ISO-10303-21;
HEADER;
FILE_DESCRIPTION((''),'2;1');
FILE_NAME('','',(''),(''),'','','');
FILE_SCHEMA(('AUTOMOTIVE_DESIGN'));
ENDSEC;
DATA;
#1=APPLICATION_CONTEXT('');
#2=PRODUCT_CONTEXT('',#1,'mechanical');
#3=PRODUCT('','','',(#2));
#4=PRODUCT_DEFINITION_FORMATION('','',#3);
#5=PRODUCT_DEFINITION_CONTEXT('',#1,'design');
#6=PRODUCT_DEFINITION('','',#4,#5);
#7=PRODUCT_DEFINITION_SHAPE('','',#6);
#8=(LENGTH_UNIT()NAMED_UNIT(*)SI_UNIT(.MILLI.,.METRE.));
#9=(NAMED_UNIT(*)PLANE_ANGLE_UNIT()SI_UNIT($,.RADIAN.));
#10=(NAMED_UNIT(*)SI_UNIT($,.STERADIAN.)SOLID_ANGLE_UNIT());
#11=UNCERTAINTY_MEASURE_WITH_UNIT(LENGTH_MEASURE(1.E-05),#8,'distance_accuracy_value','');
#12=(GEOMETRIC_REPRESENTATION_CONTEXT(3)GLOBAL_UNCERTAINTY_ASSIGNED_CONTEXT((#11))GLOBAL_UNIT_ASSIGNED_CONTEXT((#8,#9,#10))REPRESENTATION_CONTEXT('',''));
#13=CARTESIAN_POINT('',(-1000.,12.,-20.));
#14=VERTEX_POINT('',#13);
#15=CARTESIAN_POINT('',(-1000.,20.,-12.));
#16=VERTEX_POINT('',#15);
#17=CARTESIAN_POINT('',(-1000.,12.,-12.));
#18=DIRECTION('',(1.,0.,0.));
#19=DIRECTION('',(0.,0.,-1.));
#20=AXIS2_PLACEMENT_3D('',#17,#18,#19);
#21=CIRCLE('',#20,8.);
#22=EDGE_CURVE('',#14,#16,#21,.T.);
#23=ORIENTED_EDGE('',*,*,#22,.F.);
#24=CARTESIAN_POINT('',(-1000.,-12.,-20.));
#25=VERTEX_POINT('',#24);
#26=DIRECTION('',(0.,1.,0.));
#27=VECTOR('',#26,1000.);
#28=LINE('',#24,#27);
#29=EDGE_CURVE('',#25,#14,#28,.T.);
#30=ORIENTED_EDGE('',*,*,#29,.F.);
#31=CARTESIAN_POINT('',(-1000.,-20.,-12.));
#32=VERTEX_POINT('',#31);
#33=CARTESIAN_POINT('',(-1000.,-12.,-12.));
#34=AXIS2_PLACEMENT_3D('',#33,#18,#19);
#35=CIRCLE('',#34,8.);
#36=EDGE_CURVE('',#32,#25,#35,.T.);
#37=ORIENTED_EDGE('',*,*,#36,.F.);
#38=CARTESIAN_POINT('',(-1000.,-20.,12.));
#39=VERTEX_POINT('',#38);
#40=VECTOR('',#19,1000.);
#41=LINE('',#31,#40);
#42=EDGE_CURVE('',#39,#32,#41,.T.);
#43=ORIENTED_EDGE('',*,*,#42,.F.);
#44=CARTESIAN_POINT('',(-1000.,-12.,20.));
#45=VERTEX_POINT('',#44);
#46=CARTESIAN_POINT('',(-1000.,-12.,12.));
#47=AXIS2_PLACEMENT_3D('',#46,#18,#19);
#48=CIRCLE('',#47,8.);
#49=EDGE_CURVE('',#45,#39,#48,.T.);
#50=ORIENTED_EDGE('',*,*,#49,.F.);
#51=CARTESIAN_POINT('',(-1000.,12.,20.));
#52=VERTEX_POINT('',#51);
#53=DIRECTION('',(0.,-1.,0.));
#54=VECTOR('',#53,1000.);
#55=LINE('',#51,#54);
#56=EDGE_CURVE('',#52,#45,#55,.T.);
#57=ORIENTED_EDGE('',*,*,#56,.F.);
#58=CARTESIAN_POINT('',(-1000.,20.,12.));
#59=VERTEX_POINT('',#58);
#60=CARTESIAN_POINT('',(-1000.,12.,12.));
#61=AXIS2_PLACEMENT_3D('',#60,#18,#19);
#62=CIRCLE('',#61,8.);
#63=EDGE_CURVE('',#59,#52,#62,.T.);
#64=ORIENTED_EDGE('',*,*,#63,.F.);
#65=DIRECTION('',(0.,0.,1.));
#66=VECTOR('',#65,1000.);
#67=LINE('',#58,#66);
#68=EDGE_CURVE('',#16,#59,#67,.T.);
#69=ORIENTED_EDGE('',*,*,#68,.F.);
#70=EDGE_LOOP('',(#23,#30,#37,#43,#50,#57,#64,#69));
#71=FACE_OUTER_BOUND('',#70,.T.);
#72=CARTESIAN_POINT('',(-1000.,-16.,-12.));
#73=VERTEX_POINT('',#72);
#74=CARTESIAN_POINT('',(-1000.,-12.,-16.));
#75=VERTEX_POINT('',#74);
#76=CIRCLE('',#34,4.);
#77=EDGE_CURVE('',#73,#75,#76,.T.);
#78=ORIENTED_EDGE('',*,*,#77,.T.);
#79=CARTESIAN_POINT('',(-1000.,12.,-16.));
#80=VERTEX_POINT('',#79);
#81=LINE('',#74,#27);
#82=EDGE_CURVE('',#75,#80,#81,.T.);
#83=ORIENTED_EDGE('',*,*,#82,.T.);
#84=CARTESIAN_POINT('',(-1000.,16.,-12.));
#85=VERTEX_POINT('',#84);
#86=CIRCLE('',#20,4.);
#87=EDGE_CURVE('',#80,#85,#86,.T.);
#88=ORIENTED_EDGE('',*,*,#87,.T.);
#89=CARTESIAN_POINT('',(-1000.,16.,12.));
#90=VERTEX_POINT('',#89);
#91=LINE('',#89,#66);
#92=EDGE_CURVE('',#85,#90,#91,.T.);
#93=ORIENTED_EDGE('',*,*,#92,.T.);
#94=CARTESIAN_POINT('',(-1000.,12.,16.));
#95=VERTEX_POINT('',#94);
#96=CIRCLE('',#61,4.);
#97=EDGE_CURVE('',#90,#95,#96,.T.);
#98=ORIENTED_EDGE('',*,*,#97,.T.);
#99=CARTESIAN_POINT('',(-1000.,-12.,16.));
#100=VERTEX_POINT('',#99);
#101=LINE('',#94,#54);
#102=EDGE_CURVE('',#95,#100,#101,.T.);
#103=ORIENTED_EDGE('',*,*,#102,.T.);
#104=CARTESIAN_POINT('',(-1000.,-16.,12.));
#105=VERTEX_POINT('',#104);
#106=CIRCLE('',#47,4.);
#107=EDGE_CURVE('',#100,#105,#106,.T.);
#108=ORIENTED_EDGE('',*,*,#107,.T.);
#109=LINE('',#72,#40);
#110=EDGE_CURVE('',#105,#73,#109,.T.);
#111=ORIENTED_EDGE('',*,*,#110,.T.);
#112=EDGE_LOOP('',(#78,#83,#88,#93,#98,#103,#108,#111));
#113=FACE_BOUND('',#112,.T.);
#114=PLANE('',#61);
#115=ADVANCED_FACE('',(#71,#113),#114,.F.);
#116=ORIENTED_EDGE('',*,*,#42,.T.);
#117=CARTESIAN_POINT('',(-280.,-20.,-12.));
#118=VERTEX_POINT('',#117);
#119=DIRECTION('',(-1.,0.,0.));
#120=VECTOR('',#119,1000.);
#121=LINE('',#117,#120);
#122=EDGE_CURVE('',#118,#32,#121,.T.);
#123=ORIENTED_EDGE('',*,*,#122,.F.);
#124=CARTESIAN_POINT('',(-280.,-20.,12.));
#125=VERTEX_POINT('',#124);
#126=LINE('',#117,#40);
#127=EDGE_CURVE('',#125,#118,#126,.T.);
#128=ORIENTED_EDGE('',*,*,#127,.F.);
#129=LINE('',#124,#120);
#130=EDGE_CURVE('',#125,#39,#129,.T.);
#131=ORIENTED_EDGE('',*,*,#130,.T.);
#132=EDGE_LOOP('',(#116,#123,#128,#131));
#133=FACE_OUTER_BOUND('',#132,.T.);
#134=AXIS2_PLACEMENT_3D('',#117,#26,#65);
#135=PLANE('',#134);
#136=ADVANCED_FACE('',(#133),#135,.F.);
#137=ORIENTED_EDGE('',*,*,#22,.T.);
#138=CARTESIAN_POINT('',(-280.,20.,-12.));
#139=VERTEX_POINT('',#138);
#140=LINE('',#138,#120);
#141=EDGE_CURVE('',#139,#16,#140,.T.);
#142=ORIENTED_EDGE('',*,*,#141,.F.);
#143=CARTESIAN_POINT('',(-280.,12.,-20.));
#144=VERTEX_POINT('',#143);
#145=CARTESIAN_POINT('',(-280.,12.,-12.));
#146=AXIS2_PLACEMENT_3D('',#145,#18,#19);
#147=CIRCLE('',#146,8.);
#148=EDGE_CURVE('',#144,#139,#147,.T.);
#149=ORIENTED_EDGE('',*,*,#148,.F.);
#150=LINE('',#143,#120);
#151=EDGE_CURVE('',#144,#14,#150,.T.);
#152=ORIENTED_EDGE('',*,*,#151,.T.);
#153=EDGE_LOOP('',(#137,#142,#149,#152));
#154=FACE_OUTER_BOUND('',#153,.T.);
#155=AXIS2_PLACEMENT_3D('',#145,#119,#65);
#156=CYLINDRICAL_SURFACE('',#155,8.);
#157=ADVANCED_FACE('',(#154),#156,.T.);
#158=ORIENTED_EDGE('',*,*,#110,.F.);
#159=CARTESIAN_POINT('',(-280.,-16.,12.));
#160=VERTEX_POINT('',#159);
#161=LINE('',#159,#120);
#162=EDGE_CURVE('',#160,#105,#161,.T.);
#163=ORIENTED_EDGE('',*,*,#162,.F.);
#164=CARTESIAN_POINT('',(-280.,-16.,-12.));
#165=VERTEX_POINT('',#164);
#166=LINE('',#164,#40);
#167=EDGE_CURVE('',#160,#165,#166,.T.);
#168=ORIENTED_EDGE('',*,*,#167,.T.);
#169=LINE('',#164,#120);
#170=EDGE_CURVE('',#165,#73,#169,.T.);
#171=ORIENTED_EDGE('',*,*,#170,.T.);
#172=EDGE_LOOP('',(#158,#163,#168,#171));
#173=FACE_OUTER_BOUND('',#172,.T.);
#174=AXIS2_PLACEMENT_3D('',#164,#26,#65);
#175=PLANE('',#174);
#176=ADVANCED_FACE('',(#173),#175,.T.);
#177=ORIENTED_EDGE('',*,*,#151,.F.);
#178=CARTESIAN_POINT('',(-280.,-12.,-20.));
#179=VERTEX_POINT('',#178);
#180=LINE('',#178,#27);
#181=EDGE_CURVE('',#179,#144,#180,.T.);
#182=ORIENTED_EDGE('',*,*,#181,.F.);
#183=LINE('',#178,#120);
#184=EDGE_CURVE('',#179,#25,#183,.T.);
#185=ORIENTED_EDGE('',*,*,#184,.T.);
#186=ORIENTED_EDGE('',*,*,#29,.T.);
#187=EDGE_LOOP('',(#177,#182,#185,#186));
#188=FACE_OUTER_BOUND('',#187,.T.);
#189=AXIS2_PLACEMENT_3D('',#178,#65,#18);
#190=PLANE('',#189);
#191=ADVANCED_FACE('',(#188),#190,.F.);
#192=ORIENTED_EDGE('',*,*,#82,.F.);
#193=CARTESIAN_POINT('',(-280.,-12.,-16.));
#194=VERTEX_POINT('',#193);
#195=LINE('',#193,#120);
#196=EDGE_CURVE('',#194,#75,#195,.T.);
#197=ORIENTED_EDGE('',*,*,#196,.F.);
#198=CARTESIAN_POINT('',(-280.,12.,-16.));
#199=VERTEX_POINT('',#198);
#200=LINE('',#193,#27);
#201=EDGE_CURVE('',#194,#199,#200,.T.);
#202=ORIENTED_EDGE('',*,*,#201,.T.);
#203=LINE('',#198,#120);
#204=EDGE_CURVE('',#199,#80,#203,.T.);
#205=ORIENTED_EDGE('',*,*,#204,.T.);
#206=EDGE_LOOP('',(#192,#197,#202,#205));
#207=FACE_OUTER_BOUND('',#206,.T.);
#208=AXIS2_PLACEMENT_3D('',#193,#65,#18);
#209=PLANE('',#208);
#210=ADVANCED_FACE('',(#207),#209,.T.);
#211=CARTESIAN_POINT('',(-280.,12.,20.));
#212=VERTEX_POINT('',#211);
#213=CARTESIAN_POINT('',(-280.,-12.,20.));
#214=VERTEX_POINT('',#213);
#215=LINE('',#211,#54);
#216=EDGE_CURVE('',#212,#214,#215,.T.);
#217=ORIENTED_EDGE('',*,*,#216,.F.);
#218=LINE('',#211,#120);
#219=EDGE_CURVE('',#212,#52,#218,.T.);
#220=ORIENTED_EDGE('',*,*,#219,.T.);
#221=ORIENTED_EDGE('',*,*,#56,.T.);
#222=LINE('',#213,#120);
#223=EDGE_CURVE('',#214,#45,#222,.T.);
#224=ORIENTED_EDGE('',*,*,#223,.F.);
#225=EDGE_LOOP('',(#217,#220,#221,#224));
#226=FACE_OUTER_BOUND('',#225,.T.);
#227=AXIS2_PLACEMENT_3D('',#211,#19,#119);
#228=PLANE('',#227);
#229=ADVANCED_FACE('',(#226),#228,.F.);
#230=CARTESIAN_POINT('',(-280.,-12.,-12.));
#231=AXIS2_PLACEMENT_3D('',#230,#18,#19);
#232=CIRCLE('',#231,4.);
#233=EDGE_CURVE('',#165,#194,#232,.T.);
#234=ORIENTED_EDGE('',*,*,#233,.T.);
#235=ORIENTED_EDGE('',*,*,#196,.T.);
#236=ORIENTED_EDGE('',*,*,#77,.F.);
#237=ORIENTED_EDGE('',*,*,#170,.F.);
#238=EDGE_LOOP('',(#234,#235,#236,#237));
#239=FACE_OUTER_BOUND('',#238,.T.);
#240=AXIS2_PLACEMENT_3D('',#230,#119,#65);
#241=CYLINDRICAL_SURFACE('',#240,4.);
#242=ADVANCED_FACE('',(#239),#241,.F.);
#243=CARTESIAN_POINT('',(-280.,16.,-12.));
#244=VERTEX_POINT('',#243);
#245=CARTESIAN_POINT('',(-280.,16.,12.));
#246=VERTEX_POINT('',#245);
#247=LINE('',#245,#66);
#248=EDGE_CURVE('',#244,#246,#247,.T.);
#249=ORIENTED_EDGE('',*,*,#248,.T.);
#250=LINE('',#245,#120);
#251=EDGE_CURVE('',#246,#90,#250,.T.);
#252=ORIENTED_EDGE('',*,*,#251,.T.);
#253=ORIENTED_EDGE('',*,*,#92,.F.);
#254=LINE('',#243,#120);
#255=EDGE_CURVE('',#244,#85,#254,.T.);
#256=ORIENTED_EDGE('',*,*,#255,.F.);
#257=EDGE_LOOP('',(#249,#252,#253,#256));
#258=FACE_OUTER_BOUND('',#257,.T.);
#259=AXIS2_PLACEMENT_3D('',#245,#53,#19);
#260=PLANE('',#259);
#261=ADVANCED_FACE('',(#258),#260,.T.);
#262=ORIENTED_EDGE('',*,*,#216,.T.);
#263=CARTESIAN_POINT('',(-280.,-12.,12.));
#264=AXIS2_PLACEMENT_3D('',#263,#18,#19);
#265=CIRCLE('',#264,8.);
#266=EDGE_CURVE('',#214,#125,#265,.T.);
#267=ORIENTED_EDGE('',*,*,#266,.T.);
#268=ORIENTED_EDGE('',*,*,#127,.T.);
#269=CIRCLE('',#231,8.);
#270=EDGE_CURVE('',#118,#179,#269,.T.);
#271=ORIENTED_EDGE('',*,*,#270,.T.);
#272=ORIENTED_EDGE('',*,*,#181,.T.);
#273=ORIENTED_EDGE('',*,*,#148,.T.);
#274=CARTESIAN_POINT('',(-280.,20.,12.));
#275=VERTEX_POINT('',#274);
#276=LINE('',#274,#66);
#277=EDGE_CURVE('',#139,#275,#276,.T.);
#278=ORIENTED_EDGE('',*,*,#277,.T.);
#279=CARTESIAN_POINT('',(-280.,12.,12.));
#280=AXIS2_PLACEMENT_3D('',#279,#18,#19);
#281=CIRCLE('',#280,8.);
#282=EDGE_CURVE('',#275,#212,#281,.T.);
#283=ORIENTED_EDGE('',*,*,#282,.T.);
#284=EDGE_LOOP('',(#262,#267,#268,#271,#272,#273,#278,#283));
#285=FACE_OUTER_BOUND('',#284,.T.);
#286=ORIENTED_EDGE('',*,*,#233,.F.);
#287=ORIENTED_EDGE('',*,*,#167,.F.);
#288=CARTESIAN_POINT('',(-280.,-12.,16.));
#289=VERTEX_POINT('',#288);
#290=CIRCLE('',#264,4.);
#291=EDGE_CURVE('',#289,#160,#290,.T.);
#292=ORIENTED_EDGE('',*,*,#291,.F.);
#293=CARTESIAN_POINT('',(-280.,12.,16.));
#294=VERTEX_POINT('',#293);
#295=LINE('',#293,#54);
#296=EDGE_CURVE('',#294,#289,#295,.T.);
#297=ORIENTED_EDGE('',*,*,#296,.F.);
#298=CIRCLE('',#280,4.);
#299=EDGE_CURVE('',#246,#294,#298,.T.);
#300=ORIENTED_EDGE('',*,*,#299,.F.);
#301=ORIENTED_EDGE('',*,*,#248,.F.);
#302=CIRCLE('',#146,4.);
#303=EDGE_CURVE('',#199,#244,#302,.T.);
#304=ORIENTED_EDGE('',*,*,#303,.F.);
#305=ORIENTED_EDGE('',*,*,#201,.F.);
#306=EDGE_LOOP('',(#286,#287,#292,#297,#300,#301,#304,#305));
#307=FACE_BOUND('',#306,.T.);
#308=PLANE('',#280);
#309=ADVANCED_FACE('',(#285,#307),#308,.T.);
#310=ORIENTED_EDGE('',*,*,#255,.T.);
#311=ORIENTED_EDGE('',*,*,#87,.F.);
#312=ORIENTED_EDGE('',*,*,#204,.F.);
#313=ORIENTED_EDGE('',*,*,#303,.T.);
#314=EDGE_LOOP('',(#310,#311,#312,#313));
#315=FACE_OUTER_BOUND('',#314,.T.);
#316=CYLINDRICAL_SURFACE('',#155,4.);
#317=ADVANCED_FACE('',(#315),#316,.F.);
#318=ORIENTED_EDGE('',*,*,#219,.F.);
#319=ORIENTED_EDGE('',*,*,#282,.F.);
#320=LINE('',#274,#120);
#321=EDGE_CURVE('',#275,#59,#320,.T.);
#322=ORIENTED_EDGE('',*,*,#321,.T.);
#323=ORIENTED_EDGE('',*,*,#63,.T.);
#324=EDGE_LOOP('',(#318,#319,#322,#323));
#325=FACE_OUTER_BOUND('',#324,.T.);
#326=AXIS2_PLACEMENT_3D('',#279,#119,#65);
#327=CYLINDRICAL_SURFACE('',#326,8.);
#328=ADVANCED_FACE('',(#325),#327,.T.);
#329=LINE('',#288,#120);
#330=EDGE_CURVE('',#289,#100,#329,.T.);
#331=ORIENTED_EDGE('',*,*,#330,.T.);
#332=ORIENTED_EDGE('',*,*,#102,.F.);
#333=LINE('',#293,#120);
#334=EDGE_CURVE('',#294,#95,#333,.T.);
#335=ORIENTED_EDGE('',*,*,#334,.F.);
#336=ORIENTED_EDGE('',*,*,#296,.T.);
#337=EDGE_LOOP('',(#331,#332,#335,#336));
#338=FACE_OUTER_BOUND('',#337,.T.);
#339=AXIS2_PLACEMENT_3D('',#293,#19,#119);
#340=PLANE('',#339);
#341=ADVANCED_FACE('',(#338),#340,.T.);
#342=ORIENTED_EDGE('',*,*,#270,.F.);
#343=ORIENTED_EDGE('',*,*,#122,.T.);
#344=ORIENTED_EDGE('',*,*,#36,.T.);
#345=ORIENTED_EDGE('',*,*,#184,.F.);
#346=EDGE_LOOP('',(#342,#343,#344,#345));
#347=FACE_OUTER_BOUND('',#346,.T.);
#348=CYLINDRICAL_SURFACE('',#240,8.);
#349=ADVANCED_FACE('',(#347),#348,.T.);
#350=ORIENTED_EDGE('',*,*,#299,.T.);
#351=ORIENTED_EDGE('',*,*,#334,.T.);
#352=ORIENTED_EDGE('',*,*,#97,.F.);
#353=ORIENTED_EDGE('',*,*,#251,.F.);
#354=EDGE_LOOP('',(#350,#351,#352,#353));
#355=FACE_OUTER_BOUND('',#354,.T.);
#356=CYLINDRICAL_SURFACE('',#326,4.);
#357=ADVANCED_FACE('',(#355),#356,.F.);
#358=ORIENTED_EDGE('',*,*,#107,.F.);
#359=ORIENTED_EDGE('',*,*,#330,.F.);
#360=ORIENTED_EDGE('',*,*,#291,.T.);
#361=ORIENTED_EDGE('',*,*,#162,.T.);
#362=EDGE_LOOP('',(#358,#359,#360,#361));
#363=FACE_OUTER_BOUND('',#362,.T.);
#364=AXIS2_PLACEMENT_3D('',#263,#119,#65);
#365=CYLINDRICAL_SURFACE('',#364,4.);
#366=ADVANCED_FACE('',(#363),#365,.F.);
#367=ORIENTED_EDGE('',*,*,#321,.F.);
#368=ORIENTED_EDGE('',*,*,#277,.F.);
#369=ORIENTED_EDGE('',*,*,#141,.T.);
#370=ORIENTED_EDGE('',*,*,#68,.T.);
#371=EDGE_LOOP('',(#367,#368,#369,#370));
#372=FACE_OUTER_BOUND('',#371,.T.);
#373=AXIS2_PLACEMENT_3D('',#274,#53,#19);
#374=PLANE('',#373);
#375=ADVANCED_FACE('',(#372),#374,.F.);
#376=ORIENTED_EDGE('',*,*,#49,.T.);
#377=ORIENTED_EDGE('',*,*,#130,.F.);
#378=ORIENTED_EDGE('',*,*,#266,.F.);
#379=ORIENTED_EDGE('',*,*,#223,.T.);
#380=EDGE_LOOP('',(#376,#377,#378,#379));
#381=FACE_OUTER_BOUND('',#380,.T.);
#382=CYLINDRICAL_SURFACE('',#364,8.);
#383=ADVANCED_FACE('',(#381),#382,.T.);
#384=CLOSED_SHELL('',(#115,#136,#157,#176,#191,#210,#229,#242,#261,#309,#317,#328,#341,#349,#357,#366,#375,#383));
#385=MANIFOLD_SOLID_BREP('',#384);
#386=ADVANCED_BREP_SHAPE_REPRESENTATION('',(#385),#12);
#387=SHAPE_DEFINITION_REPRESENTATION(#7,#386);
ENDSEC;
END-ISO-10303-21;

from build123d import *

# Parameters (mm, degrees)
SQUARE_TUBE_40_X_40_X_4_1_DEPTH = 720


with BuildPart() as part:
    # Sketch1 → Square Tube 40 X 40 X 4(1) (new body)
    with BuildSketch(Plane.YZ.offset(-1000)):
        with BuildLine():
            Line((-12, -20), (12, -20))
            ThreePointArc((12, -20), (17.656854249, -17.656854249), (20, -12))
            Line((20, -12), (20, 12))
            ThreePointArc((20, 12), (17.656854249, 17.656854249), (12, 20))
            Line((12, 20), (-12, 20))
            ThreePointArc((-12, 20), (-17.656854249, 17.656854249), (-20, 12))
            Line((-20, 12), (-20, -12))
            ThreePointArc((-20, -12), (-17.656854249, -17.656854249), (-12, -20))
        make_face()
        with BuildLine():
            Line((-12, -16), (12, -16))
            ThreePointArc((12, -16), (14.828427125, -14.828427125), (16, -12))
            Line((16, -12), (16, 12))
            ThreePointArc((16, 12), (14.828427125, 14.828427125), (12, 16))
            Line((12, 16), (-12, 16))
            ThreePointArc((-12, 16), (-14.828427125, 14.828427125), (-16, 12))
            Line((-16, 12), (-16, -12))
            ThreePointArc((-16, -12), (-14.828427125, -14.828427125), (-12, -16))
        make_face(mode=Mode.SUBTRACT)
    extrude(amount=SQUARE_TUBE_40_X_40_X_4_1_DEPTH)


solid = part.part
